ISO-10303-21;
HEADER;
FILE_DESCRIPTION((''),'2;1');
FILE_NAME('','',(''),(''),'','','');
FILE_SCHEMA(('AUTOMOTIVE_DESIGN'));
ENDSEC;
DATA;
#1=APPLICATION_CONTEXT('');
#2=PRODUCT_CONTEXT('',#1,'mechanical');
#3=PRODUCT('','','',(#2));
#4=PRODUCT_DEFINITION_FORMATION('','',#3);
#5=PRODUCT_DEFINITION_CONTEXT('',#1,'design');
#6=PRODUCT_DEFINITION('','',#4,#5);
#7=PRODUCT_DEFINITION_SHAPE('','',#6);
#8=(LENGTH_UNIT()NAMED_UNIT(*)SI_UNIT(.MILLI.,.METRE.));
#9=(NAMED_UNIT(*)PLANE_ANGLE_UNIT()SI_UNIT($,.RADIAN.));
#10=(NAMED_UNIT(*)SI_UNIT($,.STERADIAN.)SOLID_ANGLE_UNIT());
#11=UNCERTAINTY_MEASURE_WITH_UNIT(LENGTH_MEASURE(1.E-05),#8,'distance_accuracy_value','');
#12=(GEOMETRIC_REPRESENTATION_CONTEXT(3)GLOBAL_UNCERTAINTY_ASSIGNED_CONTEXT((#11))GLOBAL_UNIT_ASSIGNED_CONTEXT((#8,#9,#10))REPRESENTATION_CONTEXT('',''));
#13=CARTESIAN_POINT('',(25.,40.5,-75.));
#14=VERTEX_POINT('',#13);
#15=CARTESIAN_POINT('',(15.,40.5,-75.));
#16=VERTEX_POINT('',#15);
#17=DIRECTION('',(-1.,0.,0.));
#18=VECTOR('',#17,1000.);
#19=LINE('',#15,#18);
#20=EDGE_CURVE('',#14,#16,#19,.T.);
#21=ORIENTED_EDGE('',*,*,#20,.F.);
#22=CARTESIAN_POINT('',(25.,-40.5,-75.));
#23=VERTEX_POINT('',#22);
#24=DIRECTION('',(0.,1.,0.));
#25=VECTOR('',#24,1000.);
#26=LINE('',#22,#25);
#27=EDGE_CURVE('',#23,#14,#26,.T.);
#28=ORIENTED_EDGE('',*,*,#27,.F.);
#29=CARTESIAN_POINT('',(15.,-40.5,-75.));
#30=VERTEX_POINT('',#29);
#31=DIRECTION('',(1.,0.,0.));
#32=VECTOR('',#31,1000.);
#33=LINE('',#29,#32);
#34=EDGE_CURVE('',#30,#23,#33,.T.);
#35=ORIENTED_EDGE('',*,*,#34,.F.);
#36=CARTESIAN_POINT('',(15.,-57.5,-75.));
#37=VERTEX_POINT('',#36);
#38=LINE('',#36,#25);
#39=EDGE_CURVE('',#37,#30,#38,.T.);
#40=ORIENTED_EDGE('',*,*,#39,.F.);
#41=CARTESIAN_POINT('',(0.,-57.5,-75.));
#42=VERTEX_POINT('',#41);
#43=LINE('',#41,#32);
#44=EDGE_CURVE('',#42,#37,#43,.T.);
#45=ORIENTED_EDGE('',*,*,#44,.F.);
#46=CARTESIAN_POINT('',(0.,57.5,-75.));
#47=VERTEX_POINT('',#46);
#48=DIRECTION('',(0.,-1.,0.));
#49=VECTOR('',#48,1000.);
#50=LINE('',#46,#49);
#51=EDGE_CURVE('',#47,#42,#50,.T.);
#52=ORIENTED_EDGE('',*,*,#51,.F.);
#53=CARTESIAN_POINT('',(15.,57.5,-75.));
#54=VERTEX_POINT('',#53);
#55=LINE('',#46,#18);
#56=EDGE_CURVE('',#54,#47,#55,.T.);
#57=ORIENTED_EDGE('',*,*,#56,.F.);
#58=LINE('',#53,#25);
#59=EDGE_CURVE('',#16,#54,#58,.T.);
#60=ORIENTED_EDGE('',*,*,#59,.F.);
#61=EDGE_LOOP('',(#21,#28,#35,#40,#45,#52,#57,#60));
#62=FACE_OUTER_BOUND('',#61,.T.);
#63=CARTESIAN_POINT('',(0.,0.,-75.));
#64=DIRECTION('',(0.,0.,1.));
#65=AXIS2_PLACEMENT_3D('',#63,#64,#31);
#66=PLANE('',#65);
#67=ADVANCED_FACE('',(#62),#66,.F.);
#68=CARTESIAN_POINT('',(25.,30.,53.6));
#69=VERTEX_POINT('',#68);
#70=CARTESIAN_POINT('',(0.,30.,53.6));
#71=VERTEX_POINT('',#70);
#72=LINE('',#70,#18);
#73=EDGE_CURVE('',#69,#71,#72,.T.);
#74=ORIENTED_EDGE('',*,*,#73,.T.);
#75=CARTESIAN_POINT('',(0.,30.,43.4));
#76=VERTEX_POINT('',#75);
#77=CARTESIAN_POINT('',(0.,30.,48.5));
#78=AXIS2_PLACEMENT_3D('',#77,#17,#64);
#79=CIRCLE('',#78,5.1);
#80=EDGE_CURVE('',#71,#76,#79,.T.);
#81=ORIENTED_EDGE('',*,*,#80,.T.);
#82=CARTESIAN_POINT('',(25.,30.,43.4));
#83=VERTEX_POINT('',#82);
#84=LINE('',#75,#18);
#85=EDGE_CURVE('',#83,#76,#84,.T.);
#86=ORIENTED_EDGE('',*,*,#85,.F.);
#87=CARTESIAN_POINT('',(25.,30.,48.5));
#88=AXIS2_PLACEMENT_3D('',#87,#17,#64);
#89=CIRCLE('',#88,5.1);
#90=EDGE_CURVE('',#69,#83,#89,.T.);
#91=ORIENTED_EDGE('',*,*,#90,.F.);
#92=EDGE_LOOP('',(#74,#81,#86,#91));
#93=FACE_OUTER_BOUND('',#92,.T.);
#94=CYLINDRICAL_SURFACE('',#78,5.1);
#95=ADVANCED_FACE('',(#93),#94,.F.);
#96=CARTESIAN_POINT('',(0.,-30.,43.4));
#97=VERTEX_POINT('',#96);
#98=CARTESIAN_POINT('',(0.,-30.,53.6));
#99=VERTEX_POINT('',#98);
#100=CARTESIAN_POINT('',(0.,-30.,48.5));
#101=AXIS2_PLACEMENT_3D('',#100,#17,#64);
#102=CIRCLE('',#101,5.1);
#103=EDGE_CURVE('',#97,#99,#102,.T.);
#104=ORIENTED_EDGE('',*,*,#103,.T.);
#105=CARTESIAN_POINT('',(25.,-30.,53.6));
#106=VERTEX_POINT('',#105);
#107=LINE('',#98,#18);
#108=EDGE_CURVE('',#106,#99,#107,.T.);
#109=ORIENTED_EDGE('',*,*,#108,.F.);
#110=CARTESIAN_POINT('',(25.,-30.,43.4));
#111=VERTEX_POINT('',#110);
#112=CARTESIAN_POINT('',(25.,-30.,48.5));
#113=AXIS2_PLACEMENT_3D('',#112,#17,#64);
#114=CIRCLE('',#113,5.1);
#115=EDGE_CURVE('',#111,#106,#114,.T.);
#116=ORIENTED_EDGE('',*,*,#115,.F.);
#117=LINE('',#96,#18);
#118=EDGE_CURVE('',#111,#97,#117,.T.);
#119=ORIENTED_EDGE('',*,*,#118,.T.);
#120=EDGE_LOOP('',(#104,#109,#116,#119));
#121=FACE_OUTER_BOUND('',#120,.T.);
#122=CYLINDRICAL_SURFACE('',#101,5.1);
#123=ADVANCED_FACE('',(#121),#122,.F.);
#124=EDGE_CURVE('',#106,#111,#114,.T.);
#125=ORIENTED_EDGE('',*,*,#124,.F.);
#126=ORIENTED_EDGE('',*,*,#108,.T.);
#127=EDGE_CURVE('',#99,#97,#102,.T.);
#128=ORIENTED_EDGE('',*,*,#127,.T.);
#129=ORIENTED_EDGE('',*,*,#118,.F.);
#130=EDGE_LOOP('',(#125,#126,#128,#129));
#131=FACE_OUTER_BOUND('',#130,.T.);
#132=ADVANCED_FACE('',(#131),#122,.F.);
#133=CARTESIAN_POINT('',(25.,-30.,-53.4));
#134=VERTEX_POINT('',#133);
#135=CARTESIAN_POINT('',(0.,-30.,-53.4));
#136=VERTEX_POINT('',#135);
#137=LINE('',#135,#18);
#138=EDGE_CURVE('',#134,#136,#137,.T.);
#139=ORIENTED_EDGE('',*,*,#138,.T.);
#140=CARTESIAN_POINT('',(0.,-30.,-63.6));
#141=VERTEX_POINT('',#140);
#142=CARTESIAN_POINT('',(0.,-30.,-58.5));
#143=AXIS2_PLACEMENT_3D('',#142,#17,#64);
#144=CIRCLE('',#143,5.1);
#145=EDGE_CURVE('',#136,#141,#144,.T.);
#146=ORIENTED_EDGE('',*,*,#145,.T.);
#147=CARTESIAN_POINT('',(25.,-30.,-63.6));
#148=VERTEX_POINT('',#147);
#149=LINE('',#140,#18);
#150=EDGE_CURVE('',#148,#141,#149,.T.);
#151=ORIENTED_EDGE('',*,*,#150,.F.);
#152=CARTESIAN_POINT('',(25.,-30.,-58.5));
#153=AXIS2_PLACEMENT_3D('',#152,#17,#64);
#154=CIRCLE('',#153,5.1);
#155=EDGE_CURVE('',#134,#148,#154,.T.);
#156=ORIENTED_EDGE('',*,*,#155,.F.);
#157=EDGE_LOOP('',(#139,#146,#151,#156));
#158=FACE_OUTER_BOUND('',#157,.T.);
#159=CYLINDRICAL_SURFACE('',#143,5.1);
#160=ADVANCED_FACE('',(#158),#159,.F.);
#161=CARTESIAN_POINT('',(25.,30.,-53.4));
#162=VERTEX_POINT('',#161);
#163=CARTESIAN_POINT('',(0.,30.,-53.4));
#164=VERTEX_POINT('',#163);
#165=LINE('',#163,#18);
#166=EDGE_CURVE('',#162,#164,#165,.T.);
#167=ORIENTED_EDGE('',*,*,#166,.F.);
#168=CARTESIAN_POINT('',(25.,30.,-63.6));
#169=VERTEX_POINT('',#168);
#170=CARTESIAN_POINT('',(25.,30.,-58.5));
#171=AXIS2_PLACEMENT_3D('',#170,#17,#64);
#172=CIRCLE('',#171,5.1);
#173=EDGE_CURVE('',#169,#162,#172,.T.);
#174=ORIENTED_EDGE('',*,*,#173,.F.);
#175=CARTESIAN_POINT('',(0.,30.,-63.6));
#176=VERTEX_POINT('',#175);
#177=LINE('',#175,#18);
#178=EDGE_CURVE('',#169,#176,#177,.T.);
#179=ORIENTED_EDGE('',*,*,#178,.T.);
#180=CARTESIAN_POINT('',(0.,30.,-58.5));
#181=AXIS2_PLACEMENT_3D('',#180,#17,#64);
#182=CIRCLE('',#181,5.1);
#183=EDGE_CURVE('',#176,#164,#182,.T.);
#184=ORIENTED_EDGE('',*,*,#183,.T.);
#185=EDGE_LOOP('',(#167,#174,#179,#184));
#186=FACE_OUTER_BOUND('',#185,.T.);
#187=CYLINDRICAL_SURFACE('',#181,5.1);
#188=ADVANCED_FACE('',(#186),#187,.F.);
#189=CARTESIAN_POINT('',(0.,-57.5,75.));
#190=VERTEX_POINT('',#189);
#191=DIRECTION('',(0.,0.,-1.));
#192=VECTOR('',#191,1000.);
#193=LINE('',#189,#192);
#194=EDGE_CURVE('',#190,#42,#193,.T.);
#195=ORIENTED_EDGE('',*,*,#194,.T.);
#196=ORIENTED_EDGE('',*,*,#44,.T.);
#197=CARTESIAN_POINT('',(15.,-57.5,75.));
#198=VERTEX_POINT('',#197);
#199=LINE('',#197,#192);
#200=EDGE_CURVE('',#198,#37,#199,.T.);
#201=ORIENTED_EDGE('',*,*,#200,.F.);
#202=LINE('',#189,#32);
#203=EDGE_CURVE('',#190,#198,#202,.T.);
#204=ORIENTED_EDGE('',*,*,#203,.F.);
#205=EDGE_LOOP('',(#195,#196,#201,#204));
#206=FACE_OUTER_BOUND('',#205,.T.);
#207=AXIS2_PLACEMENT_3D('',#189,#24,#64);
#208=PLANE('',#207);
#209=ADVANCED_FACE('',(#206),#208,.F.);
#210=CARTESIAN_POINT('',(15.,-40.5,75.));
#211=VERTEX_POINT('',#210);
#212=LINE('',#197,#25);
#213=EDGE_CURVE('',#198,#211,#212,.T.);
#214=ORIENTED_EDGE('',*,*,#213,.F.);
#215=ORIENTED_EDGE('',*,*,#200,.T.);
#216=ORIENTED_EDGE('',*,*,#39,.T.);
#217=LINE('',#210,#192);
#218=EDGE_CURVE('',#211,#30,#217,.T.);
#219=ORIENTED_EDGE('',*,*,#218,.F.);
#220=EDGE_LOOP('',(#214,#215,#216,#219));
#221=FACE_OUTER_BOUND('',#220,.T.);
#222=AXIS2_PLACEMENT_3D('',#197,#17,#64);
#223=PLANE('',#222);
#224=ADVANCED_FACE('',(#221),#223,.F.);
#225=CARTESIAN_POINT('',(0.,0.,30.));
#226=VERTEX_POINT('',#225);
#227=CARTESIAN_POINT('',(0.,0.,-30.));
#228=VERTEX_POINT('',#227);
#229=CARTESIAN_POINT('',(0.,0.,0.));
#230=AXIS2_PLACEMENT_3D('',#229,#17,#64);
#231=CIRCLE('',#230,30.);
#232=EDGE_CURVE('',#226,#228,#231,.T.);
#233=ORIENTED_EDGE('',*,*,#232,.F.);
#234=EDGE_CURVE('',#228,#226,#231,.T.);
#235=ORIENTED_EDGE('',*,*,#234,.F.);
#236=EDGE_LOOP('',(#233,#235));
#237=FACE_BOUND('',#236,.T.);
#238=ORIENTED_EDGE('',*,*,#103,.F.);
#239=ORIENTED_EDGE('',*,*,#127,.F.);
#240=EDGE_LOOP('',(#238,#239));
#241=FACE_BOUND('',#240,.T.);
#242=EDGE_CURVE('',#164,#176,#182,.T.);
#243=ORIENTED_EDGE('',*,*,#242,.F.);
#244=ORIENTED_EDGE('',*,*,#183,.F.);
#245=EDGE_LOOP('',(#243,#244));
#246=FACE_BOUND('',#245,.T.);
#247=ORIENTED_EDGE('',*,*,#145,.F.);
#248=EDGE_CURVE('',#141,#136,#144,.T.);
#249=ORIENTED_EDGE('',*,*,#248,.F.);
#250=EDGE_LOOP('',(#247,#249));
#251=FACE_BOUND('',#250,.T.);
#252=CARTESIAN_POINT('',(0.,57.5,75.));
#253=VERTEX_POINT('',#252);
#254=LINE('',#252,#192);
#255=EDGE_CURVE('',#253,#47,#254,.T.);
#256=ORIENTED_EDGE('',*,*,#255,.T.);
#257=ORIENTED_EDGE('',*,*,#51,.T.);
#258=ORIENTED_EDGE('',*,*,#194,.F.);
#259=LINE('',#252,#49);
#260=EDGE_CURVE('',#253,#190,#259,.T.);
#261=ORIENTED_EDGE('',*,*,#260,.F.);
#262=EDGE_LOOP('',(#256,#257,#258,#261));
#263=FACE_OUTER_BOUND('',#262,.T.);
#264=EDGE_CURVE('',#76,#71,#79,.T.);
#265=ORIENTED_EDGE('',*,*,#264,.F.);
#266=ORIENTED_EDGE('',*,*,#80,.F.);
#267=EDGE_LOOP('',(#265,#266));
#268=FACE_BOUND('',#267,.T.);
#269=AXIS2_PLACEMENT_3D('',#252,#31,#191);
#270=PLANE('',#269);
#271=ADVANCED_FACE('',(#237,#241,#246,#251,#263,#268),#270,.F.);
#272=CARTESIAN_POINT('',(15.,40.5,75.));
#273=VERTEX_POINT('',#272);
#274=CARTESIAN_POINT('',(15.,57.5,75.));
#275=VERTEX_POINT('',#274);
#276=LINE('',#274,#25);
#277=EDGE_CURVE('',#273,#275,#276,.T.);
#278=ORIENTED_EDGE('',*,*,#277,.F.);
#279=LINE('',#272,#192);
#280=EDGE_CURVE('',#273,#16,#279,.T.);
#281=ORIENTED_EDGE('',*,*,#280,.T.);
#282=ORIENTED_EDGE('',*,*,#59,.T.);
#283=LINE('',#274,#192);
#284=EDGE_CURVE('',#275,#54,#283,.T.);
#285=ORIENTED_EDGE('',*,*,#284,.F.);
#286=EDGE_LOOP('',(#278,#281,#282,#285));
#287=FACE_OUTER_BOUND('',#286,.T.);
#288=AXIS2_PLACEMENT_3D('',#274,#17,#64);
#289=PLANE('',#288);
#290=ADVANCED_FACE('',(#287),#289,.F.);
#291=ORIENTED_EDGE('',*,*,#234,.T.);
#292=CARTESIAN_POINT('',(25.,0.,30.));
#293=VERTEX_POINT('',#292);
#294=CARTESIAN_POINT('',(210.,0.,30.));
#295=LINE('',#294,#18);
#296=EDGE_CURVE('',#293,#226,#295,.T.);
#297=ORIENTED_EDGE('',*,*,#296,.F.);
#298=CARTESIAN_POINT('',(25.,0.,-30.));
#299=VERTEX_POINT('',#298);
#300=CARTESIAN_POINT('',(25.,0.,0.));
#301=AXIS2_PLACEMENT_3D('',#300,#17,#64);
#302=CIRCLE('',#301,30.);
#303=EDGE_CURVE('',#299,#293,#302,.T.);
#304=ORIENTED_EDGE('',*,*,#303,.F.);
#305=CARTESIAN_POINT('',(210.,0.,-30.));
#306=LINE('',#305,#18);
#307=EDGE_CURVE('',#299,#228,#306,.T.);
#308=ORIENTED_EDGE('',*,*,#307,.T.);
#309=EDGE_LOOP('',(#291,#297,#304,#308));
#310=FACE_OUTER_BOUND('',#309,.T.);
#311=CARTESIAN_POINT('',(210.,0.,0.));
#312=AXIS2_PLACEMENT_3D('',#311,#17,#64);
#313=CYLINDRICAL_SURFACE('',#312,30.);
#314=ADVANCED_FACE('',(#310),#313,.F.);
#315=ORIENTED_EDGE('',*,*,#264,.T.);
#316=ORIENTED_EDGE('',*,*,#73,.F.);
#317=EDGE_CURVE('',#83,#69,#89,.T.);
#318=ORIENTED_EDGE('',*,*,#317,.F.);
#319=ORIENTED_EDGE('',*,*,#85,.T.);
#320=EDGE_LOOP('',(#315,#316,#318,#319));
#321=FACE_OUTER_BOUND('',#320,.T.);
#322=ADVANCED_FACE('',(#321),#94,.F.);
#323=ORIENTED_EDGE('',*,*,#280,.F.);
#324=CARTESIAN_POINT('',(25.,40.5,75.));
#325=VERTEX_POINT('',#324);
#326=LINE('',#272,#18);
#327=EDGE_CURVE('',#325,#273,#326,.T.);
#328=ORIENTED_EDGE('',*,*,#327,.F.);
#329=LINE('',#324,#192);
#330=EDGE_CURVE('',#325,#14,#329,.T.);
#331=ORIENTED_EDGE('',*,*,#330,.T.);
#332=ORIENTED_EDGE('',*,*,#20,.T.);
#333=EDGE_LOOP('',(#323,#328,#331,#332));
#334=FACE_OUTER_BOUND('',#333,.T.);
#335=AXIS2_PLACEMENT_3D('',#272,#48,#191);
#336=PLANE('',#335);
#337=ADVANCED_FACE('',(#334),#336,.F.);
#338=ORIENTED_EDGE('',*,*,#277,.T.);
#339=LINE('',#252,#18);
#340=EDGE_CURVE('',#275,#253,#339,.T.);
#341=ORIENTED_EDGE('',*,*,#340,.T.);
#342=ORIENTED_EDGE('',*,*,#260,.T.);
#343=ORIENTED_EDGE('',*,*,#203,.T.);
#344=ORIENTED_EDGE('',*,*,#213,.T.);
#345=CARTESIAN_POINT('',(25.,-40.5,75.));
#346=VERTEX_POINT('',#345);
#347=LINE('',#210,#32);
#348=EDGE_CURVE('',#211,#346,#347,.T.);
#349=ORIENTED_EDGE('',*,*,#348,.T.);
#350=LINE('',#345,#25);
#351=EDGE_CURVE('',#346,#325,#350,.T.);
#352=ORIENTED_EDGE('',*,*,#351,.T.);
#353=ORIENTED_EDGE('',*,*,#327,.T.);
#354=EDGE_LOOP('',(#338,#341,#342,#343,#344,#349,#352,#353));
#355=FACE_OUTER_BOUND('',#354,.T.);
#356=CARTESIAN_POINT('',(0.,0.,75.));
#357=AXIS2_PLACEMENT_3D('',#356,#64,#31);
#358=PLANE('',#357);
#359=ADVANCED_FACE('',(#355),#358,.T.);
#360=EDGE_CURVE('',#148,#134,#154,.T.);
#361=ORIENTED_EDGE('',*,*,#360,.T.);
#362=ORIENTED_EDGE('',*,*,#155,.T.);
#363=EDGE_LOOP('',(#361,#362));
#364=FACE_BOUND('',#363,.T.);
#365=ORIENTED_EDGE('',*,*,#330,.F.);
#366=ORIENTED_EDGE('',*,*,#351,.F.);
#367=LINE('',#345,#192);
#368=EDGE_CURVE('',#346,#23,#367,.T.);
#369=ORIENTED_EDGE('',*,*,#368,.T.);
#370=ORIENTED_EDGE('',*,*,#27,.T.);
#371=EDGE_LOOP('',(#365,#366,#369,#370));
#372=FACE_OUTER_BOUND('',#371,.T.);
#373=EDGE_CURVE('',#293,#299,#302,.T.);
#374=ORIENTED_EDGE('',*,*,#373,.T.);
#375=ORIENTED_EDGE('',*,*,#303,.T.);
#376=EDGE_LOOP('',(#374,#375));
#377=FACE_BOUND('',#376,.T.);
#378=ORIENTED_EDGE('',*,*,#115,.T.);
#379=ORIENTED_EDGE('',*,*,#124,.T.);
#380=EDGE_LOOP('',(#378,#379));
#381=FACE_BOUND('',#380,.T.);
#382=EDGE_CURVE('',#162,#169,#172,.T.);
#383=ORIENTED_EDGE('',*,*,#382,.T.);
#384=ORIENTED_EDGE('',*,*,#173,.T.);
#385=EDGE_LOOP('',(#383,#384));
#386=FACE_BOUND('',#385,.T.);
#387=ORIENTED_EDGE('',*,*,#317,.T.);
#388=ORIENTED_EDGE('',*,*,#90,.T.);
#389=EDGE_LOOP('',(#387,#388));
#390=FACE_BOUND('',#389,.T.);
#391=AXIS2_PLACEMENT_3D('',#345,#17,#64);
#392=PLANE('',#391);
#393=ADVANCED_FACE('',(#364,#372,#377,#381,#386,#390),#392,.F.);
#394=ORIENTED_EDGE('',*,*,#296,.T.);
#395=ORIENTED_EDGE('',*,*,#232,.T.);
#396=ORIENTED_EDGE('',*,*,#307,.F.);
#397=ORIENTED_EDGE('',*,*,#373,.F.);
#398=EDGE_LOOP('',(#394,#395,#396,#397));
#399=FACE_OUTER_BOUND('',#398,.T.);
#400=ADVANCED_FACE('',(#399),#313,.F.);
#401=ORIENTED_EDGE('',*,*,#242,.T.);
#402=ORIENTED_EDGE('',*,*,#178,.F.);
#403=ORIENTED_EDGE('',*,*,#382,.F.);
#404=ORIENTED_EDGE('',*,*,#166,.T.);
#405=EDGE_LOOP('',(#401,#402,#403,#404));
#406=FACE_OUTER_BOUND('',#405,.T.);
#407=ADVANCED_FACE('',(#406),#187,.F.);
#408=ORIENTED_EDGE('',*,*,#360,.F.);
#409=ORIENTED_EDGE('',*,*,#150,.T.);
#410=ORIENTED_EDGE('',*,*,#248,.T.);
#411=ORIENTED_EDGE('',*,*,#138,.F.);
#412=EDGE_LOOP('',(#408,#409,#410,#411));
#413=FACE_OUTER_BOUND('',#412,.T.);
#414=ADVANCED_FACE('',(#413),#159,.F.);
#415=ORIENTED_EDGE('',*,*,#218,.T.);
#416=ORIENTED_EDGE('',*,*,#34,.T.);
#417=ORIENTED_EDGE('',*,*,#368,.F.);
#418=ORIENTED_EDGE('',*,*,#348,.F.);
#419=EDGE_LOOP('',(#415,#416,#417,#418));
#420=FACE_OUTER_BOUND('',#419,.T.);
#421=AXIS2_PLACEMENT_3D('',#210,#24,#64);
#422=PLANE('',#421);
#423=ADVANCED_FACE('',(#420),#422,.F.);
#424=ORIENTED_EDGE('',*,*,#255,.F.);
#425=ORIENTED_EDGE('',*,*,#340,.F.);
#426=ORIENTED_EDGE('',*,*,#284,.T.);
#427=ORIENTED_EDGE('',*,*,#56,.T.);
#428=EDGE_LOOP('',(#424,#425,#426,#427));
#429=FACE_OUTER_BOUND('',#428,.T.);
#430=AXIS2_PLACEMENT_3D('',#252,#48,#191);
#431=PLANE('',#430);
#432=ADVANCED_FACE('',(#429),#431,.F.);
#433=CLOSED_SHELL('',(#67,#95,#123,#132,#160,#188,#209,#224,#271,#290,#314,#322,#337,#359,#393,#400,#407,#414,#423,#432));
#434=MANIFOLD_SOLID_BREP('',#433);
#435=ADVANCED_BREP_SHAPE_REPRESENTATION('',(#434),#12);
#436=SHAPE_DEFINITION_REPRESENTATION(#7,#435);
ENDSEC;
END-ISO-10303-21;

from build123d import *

# Parameters (mm, degrees)
EXTRUDE_1_DEPTH     = 75
SKETCH_2_R          = 30
CUT_EXTRUDE_1_DEPTH = 210
HOLE_WIZARD_M12_1_D = 10.2


with BuildPart() as part:
    # 草图1 → 凸台-拉伸1 (new, symmetric)
    with BuildSketch(Plane.XY):
        Polygon((0, 57.5), (0, -57.5), (15, -57.5), (15, -40.5), (25, -40.5), (25, 40.5), (15, 40.5), (15, 57.5), align=None)
    extrude(amount=EXTRUDE_1_DEPTH, both=True)

    # 草图2 → 切除-拉伸1 (cut)
    with BuildSketch(Plane.ZY):
        Circle(SKETCH_2_R)
    extrude(amount=-CUT_EXTRUDE_1_DEPTH, mode=Mode.SUBTRACT)

    # M12 螺纹孔1 (through all)
    with Locations(Plane.ZY):
        with Locations((-58.5, 30), (48.5, 30), (48.5, -30), (-58.5, -30)):
            Hole(HOLE_WIZARD_M12_1_D / 2)


solid = part.part
